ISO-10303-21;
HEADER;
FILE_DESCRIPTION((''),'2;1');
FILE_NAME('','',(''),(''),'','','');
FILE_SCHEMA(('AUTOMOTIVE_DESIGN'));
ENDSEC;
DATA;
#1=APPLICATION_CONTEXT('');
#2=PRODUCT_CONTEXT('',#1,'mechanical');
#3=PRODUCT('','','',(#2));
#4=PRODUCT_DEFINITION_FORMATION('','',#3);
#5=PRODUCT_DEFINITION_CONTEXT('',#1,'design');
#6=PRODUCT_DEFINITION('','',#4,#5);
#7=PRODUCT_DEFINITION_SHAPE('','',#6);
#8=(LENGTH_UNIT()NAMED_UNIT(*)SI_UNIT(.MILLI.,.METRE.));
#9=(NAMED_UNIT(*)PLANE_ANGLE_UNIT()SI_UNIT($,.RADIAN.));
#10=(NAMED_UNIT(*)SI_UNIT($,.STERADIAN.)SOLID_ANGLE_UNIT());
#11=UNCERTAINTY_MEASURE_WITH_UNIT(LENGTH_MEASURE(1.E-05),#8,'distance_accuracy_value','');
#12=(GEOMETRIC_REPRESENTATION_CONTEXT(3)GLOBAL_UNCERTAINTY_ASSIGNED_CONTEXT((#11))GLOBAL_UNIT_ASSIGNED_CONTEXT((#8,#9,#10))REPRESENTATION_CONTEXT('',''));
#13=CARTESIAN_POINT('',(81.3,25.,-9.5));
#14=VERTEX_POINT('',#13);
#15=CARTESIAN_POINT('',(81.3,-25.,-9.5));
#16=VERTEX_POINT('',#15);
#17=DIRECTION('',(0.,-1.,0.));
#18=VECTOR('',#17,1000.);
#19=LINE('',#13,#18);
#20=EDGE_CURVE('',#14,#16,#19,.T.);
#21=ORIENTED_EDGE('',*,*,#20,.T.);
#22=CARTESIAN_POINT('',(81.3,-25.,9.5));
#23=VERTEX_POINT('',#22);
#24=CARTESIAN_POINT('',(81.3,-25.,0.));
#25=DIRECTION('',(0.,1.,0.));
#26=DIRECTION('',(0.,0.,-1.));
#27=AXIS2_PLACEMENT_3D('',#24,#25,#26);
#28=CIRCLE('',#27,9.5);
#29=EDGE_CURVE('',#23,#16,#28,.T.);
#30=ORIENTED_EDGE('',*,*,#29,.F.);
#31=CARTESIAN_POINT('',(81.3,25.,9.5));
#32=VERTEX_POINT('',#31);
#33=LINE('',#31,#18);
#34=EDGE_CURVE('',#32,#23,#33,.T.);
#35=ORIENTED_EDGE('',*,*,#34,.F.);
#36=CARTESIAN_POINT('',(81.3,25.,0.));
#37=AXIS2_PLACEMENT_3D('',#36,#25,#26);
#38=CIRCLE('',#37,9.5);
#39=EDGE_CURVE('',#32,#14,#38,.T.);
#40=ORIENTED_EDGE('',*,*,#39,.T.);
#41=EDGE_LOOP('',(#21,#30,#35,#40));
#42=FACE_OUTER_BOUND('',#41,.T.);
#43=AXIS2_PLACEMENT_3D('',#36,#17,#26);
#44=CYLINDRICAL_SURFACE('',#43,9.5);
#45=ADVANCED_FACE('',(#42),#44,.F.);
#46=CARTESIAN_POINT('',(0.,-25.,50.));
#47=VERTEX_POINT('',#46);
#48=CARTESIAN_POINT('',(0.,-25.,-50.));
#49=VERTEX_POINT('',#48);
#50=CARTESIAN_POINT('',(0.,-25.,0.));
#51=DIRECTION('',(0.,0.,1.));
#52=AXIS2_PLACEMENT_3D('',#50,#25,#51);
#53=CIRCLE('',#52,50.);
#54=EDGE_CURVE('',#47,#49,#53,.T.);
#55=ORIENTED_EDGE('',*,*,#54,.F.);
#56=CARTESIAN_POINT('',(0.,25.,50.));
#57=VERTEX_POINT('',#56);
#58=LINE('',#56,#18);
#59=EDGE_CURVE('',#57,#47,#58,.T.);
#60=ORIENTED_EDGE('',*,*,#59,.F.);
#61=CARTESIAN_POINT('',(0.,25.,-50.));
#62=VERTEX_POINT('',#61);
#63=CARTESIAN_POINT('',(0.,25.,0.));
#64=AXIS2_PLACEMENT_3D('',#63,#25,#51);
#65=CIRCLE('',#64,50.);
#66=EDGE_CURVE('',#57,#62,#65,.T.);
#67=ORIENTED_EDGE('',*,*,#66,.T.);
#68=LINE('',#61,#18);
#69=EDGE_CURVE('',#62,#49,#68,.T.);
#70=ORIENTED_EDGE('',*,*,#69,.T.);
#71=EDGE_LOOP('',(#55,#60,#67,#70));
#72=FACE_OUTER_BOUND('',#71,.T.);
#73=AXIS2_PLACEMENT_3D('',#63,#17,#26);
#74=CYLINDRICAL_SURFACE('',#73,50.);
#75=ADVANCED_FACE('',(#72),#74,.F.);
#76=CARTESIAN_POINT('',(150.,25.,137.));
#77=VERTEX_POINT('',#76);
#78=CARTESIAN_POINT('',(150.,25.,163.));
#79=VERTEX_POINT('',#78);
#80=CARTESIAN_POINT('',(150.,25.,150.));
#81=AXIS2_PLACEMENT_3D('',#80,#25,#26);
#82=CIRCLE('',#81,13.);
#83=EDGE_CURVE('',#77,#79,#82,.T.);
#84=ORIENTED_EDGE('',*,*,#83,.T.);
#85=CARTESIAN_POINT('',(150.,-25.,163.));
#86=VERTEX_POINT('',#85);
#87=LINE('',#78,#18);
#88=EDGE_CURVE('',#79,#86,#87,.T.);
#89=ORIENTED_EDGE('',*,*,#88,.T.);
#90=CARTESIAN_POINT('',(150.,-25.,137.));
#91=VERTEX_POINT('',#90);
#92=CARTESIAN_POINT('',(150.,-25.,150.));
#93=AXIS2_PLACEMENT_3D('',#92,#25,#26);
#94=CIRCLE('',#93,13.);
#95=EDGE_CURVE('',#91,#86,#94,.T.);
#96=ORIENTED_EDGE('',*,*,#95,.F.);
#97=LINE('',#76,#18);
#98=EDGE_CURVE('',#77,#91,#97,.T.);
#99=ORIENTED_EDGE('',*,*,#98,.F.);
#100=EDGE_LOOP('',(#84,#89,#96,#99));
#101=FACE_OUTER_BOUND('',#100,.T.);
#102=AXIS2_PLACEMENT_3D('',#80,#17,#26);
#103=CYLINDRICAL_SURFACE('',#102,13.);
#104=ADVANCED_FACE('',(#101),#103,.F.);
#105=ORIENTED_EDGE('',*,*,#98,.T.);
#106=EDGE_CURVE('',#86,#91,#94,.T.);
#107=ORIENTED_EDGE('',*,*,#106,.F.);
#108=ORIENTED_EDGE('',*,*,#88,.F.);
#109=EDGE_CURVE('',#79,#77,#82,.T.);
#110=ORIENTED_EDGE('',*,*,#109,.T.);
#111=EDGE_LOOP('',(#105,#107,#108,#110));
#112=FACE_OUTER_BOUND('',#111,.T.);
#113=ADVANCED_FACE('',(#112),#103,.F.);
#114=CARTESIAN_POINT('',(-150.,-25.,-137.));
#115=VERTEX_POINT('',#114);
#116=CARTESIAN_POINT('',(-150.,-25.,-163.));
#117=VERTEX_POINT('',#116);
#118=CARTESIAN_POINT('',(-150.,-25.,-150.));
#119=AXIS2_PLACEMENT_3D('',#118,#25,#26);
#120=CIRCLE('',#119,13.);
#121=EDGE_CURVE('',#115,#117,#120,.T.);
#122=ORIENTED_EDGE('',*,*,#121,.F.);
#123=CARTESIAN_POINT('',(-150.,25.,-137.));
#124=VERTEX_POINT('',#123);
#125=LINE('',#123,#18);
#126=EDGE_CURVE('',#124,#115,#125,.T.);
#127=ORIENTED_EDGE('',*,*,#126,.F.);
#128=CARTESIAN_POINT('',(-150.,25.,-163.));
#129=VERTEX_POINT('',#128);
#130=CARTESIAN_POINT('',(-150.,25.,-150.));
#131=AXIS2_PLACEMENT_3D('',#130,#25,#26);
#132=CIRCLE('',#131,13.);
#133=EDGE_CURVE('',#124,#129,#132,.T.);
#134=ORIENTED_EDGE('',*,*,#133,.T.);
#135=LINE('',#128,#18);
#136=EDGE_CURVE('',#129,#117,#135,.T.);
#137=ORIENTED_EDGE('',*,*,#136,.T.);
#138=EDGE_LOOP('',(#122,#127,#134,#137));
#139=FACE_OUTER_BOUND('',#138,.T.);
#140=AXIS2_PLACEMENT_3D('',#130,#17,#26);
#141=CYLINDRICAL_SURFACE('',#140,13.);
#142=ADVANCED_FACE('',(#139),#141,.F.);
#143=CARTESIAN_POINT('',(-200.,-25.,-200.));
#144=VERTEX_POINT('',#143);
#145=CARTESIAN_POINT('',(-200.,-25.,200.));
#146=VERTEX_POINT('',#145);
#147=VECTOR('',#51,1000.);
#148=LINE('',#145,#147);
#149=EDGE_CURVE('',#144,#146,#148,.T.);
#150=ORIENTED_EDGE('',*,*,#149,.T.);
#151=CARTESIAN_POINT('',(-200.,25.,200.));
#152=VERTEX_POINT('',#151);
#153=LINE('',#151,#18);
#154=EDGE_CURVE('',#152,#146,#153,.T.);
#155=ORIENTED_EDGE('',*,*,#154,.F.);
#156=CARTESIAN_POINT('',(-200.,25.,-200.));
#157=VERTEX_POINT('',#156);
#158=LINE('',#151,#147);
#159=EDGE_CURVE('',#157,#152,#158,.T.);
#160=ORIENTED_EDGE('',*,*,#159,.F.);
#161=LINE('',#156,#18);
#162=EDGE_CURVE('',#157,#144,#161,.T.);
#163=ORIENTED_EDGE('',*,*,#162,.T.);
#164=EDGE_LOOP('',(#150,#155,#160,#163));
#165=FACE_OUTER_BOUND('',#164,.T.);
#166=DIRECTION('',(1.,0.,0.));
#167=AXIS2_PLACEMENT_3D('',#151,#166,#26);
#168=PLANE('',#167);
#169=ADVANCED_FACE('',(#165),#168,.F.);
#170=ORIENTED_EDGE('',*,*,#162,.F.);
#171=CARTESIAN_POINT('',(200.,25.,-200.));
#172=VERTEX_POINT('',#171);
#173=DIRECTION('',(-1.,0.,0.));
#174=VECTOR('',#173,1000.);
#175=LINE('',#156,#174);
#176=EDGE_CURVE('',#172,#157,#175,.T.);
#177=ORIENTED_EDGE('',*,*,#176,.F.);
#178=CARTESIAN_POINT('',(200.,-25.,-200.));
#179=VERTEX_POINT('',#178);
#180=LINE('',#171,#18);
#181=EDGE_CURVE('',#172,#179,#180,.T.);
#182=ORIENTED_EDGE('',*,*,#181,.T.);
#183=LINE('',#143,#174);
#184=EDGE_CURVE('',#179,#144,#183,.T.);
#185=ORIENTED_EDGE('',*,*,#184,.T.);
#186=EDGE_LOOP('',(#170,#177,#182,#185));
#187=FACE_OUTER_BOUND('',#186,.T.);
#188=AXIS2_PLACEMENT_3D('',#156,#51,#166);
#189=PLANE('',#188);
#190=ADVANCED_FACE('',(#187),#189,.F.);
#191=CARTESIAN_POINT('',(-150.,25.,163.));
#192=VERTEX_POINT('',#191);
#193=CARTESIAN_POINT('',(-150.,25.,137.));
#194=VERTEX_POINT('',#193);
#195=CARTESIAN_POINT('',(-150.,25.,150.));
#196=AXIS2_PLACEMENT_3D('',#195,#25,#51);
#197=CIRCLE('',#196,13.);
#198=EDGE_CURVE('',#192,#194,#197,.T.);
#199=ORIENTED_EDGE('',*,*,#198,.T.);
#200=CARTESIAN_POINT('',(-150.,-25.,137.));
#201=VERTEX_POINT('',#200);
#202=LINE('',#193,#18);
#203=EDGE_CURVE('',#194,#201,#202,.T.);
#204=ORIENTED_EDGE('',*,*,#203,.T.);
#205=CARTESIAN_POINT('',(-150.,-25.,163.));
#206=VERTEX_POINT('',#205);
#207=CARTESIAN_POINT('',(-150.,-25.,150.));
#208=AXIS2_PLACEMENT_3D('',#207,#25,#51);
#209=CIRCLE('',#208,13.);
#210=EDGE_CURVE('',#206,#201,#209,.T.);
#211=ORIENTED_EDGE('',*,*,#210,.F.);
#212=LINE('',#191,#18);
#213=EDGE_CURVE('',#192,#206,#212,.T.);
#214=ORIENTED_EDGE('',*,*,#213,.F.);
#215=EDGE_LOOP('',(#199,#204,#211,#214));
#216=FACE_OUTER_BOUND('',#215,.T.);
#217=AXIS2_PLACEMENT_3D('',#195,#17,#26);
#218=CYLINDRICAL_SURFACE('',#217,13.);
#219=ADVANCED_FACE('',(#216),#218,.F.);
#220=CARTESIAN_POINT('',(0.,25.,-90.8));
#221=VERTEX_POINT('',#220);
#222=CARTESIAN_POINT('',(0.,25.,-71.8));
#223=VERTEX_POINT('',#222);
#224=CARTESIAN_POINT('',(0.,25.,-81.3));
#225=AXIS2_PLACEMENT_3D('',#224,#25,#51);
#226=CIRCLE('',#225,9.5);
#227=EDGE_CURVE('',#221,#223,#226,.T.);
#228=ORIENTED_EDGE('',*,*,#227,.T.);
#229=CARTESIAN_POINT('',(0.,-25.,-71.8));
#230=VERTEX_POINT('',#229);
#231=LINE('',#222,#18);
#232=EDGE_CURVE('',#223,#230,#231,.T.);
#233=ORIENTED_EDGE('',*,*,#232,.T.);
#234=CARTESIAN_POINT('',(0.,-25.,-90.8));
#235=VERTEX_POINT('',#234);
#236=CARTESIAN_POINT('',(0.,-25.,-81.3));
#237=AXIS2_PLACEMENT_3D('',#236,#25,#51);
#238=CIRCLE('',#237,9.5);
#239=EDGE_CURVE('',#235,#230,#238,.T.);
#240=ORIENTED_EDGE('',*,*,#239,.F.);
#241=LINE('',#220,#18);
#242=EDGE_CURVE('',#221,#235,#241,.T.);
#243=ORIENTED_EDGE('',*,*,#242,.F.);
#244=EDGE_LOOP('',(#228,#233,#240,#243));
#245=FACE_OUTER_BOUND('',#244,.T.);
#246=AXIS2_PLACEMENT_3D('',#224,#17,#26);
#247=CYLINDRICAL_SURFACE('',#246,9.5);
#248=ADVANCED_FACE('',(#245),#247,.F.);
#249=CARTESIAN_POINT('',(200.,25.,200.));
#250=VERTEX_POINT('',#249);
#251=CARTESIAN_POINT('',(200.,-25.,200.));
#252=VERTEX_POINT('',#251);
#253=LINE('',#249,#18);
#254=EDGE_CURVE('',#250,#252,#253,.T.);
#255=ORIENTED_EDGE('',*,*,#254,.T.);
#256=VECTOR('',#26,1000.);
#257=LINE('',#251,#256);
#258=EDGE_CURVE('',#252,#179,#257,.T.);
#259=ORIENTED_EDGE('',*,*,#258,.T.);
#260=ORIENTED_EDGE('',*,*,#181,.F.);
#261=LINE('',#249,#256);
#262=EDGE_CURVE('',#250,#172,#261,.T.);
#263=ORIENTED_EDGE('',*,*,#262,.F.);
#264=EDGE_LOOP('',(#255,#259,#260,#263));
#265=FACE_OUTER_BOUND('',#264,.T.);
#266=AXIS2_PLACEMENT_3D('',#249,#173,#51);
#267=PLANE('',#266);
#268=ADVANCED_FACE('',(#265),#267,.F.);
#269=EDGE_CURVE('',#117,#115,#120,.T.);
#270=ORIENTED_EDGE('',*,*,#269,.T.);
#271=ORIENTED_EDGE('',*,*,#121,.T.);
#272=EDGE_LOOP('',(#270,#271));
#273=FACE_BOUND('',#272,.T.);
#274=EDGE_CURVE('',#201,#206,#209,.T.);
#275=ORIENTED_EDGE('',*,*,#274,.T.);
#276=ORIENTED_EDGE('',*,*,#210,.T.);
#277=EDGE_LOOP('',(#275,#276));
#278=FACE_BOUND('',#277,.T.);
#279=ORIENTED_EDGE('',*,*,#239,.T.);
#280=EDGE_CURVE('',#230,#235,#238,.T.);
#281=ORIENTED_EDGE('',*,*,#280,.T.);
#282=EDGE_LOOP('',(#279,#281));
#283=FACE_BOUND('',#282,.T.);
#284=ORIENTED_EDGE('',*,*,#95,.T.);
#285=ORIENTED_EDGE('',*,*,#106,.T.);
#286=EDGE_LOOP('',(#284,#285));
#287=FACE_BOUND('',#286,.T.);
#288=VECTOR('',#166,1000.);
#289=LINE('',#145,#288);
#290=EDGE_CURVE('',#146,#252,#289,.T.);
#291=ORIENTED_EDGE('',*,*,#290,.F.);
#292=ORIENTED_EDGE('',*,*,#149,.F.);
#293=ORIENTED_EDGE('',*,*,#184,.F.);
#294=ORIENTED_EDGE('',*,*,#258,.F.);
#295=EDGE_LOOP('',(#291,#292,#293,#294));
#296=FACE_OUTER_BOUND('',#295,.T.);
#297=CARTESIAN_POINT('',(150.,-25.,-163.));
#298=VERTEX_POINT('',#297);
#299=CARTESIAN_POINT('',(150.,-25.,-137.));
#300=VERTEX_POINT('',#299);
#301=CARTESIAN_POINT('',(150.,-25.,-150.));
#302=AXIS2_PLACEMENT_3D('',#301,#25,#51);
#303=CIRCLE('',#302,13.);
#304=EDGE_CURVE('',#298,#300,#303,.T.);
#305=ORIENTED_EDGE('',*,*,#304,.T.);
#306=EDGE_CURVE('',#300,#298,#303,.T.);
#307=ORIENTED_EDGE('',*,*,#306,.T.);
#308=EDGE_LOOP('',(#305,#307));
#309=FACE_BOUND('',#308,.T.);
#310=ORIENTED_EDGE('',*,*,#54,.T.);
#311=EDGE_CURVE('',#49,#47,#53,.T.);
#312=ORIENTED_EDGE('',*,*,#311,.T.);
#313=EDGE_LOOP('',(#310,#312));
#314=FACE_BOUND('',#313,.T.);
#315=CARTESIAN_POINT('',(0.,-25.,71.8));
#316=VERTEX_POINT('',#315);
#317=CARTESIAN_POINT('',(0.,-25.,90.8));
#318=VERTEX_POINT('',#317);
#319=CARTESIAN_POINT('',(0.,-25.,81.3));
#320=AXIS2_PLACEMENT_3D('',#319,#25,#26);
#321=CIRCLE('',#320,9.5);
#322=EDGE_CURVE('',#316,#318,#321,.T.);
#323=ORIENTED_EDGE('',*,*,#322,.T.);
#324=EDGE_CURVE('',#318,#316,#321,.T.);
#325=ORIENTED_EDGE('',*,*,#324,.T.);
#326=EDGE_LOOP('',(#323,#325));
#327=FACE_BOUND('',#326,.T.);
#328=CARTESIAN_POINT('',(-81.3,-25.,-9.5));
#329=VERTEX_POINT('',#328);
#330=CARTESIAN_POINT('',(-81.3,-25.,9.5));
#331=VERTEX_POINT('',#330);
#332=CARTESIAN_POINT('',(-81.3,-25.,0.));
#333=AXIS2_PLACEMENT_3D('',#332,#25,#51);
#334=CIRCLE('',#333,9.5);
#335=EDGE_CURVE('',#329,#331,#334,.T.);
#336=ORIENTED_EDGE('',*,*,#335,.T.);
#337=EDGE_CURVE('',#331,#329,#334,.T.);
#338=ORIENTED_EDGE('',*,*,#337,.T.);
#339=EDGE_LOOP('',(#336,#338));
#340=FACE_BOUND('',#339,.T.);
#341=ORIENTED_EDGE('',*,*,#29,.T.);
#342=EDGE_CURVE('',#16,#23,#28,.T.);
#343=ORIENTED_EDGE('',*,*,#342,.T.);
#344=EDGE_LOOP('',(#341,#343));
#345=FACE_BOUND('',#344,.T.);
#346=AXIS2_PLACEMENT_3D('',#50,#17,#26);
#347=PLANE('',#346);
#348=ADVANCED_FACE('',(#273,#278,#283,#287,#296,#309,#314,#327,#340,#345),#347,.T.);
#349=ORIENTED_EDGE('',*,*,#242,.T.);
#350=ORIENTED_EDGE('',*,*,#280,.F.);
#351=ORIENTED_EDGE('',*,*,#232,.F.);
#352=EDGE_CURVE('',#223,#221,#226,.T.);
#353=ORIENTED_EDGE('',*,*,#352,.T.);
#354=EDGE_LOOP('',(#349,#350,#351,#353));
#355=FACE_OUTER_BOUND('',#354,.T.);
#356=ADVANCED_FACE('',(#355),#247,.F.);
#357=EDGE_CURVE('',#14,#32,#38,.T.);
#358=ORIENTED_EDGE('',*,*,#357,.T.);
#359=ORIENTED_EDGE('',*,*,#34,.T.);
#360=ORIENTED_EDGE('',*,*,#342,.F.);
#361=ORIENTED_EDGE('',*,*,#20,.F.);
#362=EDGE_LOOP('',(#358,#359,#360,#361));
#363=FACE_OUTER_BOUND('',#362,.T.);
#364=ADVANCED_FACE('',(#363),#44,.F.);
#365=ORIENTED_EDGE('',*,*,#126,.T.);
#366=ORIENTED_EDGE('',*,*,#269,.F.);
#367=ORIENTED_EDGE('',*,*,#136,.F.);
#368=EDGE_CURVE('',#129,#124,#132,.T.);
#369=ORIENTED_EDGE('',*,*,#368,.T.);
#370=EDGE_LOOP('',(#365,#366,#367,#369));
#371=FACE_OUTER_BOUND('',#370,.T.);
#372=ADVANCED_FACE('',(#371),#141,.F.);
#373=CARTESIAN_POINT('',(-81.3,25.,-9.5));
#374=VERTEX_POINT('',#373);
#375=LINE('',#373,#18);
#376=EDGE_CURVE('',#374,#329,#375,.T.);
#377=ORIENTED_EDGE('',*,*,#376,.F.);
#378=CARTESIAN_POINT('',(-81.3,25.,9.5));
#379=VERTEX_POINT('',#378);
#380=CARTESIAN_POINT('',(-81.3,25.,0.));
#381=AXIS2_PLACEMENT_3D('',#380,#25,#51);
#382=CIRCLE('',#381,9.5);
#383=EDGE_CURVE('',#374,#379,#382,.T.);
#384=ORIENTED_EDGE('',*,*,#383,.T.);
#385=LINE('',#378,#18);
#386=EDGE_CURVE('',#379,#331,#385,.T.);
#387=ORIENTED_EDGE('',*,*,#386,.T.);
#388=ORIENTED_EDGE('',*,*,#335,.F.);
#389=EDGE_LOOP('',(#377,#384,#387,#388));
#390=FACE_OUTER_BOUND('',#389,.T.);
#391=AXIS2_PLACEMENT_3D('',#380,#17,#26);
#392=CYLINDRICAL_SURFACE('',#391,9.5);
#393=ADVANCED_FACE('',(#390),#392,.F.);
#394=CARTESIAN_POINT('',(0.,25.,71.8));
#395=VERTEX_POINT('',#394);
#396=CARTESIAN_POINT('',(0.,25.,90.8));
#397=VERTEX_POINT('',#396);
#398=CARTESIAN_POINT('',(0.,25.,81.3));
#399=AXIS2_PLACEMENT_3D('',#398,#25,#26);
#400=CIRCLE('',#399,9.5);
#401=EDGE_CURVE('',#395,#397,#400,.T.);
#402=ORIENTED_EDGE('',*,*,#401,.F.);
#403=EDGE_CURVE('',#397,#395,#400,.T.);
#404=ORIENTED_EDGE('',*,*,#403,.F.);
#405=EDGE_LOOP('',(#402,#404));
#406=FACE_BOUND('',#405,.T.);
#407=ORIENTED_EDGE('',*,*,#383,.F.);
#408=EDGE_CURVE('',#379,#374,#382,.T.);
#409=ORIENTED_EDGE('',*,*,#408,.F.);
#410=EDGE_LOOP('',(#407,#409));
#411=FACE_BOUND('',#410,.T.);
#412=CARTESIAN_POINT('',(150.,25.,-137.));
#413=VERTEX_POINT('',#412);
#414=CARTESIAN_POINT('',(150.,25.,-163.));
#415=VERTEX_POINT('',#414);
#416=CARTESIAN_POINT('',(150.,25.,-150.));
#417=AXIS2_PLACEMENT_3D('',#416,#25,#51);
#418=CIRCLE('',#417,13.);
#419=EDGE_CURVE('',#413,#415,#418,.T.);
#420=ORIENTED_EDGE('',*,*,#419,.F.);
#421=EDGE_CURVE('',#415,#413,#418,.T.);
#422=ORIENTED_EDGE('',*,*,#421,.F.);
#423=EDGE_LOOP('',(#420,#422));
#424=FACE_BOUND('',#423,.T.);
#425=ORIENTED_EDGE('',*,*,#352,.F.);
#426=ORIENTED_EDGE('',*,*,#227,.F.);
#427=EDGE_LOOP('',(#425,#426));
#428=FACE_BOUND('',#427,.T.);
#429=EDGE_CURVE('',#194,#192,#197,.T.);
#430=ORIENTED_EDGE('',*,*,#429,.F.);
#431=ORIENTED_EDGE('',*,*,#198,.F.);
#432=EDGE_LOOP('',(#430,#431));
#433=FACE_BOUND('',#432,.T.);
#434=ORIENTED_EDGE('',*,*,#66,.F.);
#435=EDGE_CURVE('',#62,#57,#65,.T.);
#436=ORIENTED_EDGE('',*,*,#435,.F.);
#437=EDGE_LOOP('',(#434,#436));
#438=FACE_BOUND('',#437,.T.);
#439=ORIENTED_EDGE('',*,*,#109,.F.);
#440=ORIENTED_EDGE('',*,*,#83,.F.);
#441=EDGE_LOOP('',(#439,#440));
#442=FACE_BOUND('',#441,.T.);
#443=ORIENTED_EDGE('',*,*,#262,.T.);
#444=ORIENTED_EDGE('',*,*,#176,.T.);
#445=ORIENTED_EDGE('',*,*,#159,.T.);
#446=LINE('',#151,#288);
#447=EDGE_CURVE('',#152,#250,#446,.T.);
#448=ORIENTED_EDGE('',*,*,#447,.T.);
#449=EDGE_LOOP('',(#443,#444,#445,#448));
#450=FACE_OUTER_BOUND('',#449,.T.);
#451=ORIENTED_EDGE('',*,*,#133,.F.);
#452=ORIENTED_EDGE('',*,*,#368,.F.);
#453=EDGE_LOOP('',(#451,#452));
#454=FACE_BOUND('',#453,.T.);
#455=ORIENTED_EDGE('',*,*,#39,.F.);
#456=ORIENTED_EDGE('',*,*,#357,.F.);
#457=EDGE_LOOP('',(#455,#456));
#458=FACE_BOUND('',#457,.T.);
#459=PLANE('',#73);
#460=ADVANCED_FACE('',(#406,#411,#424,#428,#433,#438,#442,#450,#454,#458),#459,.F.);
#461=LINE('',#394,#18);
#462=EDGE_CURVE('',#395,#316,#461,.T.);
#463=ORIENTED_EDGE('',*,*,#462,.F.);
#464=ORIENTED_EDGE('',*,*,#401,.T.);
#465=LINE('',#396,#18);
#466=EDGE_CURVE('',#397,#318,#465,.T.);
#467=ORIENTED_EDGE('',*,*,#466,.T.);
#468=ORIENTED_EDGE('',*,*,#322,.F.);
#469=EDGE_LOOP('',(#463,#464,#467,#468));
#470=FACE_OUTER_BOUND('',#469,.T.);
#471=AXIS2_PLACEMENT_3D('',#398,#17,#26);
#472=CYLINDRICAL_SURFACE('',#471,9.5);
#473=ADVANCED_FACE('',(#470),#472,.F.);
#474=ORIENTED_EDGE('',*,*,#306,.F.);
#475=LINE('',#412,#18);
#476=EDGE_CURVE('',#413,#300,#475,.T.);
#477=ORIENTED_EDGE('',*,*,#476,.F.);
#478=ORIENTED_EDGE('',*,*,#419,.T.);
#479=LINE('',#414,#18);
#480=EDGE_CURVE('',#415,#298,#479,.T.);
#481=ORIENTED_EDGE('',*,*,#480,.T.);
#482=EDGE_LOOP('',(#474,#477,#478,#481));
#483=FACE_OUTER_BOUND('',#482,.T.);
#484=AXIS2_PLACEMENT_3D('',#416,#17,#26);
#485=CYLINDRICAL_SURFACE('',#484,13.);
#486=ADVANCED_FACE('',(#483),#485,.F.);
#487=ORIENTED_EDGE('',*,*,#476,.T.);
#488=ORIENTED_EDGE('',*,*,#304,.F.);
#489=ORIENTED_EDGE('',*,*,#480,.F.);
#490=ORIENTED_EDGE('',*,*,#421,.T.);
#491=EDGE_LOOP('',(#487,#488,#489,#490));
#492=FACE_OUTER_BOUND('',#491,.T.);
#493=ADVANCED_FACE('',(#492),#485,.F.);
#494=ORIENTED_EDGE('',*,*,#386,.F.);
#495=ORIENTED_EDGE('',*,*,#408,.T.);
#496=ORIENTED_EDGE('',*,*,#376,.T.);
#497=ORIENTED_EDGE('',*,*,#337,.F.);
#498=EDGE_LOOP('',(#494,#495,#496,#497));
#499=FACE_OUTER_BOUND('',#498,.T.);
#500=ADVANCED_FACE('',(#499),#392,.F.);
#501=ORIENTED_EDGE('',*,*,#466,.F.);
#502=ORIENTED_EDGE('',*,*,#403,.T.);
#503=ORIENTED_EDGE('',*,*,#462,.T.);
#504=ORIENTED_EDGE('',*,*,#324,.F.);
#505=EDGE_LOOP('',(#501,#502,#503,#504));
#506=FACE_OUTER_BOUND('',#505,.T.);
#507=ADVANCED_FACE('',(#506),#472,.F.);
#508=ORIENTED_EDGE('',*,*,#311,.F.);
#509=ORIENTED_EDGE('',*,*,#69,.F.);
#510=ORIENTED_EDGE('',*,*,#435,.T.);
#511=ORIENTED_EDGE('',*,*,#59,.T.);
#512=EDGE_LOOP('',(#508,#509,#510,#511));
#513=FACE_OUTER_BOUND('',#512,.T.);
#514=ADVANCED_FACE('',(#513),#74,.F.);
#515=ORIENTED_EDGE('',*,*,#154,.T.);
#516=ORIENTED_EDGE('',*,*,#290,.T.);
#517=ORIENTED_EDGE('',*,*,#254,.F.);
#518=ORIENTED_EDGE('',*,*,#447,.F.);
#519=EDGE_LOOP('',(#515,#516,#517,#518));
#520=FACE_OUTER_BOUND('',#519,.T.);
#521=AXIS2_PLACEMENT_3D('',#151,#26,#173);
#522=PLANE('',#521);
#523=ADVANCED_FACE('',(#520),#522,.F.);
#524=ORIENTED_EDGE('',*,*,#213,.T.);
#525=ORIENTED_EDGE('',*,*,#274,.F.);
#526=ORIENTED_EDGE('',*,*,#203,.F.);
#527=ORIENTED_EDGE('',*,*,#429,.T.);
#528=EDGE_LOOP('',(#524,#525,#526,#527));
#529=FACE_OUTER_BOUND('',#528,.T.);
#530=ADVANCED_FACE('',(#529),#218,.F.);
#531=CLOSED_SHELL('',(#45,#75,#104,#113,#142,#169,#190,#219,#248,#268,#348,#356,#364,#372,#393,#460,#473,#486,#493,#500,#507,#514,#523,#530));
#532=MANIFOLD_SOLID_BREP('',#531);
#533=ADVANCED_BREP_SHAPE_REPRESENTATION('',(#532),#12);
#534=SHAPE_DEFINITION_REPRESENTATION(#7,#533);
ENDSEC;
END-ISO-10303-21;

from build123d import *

# Parameters (mm, degrees)
BASE_PLATE_PROFILE_W        = 400
BASE_PLATE_PROFILE_H        = 400
BASE_PLATE_PROFILE_R        = 50
BASE_PLATE_PROFILE_R_2      = 13
BASE_PLATE_PROFILE_R_3      = 9.5
BASE_PLATE_400X400X50_DEPTH = 25


with BuildPart() as part:
    # Base Plate Profile → Base Plate 400x400x50 (new, symmetric)
    with BuildSketch(Plane(origin=(0, 0, 0), x_dir=(1, 0, 0), z_dir=(0, 1, 0))):
        Rectangle(BASE_PLATE_PROFILE_W, BASE_PLATE_PROFILE_H)
        with Locations(Location((0, 0, 0), (0, 0, 270))):
            Circle(BASE_PLATE_PROFILE_R, mode=Mode.SUBTRACT)
        with Locations(Location((150, 150, 0), (0, 0, 270))):
            Circle(BASE_PLATE_PROFILE_R_2, mode=Mode.SUBTRACT)
        with Locations(Location((-150, 150, 0), (0, 0, 90))):
            Circle(BASE_PLATE_PROFILE_R_2, mode=Mode.SUBTRACT)
        with Locations(Location((150, -150, 0), (0, 0, 90))):
            Circle(BASE_PLATE_PROFILE_R_2, mode=Mode.SUBTRACT)
        with Locations(Location((-150, -150, 0), (0, 0, 270))):
            Circle(BASE_PLATE_PROFILE_R_2, mode=Mode.SUBTRACT)
        with Locations(Location((0, 81.3, 0), (0, 0, 270))):
            Circle(BASE_PLATE_PROFILE_R_3, mode=Mode.SUBTRACT)
        with Locations(Location((0, -81.3, 0), (0, 0, 90))):
            Circle(BASE_PLATE_PROFILE_R_3, mode=Mode.SUBTRACT)
        with Locations(Location((-81.3, 0, 0), (0, 0, 270))):
            Circle(BASE_PLATE_PROFILE_R_3, mode=Mode.SUBTRACT)
        with Locations(Location((81.3, 0, 0), (0, 0, 90))):
            Circle(BASE_PLATE_PROFILE_R_3, mode=Mode.SUBTRACT)
    extrude(amount=BASE_PLATE_400X400X50_DEPTH, both=True)


solid = part.part
